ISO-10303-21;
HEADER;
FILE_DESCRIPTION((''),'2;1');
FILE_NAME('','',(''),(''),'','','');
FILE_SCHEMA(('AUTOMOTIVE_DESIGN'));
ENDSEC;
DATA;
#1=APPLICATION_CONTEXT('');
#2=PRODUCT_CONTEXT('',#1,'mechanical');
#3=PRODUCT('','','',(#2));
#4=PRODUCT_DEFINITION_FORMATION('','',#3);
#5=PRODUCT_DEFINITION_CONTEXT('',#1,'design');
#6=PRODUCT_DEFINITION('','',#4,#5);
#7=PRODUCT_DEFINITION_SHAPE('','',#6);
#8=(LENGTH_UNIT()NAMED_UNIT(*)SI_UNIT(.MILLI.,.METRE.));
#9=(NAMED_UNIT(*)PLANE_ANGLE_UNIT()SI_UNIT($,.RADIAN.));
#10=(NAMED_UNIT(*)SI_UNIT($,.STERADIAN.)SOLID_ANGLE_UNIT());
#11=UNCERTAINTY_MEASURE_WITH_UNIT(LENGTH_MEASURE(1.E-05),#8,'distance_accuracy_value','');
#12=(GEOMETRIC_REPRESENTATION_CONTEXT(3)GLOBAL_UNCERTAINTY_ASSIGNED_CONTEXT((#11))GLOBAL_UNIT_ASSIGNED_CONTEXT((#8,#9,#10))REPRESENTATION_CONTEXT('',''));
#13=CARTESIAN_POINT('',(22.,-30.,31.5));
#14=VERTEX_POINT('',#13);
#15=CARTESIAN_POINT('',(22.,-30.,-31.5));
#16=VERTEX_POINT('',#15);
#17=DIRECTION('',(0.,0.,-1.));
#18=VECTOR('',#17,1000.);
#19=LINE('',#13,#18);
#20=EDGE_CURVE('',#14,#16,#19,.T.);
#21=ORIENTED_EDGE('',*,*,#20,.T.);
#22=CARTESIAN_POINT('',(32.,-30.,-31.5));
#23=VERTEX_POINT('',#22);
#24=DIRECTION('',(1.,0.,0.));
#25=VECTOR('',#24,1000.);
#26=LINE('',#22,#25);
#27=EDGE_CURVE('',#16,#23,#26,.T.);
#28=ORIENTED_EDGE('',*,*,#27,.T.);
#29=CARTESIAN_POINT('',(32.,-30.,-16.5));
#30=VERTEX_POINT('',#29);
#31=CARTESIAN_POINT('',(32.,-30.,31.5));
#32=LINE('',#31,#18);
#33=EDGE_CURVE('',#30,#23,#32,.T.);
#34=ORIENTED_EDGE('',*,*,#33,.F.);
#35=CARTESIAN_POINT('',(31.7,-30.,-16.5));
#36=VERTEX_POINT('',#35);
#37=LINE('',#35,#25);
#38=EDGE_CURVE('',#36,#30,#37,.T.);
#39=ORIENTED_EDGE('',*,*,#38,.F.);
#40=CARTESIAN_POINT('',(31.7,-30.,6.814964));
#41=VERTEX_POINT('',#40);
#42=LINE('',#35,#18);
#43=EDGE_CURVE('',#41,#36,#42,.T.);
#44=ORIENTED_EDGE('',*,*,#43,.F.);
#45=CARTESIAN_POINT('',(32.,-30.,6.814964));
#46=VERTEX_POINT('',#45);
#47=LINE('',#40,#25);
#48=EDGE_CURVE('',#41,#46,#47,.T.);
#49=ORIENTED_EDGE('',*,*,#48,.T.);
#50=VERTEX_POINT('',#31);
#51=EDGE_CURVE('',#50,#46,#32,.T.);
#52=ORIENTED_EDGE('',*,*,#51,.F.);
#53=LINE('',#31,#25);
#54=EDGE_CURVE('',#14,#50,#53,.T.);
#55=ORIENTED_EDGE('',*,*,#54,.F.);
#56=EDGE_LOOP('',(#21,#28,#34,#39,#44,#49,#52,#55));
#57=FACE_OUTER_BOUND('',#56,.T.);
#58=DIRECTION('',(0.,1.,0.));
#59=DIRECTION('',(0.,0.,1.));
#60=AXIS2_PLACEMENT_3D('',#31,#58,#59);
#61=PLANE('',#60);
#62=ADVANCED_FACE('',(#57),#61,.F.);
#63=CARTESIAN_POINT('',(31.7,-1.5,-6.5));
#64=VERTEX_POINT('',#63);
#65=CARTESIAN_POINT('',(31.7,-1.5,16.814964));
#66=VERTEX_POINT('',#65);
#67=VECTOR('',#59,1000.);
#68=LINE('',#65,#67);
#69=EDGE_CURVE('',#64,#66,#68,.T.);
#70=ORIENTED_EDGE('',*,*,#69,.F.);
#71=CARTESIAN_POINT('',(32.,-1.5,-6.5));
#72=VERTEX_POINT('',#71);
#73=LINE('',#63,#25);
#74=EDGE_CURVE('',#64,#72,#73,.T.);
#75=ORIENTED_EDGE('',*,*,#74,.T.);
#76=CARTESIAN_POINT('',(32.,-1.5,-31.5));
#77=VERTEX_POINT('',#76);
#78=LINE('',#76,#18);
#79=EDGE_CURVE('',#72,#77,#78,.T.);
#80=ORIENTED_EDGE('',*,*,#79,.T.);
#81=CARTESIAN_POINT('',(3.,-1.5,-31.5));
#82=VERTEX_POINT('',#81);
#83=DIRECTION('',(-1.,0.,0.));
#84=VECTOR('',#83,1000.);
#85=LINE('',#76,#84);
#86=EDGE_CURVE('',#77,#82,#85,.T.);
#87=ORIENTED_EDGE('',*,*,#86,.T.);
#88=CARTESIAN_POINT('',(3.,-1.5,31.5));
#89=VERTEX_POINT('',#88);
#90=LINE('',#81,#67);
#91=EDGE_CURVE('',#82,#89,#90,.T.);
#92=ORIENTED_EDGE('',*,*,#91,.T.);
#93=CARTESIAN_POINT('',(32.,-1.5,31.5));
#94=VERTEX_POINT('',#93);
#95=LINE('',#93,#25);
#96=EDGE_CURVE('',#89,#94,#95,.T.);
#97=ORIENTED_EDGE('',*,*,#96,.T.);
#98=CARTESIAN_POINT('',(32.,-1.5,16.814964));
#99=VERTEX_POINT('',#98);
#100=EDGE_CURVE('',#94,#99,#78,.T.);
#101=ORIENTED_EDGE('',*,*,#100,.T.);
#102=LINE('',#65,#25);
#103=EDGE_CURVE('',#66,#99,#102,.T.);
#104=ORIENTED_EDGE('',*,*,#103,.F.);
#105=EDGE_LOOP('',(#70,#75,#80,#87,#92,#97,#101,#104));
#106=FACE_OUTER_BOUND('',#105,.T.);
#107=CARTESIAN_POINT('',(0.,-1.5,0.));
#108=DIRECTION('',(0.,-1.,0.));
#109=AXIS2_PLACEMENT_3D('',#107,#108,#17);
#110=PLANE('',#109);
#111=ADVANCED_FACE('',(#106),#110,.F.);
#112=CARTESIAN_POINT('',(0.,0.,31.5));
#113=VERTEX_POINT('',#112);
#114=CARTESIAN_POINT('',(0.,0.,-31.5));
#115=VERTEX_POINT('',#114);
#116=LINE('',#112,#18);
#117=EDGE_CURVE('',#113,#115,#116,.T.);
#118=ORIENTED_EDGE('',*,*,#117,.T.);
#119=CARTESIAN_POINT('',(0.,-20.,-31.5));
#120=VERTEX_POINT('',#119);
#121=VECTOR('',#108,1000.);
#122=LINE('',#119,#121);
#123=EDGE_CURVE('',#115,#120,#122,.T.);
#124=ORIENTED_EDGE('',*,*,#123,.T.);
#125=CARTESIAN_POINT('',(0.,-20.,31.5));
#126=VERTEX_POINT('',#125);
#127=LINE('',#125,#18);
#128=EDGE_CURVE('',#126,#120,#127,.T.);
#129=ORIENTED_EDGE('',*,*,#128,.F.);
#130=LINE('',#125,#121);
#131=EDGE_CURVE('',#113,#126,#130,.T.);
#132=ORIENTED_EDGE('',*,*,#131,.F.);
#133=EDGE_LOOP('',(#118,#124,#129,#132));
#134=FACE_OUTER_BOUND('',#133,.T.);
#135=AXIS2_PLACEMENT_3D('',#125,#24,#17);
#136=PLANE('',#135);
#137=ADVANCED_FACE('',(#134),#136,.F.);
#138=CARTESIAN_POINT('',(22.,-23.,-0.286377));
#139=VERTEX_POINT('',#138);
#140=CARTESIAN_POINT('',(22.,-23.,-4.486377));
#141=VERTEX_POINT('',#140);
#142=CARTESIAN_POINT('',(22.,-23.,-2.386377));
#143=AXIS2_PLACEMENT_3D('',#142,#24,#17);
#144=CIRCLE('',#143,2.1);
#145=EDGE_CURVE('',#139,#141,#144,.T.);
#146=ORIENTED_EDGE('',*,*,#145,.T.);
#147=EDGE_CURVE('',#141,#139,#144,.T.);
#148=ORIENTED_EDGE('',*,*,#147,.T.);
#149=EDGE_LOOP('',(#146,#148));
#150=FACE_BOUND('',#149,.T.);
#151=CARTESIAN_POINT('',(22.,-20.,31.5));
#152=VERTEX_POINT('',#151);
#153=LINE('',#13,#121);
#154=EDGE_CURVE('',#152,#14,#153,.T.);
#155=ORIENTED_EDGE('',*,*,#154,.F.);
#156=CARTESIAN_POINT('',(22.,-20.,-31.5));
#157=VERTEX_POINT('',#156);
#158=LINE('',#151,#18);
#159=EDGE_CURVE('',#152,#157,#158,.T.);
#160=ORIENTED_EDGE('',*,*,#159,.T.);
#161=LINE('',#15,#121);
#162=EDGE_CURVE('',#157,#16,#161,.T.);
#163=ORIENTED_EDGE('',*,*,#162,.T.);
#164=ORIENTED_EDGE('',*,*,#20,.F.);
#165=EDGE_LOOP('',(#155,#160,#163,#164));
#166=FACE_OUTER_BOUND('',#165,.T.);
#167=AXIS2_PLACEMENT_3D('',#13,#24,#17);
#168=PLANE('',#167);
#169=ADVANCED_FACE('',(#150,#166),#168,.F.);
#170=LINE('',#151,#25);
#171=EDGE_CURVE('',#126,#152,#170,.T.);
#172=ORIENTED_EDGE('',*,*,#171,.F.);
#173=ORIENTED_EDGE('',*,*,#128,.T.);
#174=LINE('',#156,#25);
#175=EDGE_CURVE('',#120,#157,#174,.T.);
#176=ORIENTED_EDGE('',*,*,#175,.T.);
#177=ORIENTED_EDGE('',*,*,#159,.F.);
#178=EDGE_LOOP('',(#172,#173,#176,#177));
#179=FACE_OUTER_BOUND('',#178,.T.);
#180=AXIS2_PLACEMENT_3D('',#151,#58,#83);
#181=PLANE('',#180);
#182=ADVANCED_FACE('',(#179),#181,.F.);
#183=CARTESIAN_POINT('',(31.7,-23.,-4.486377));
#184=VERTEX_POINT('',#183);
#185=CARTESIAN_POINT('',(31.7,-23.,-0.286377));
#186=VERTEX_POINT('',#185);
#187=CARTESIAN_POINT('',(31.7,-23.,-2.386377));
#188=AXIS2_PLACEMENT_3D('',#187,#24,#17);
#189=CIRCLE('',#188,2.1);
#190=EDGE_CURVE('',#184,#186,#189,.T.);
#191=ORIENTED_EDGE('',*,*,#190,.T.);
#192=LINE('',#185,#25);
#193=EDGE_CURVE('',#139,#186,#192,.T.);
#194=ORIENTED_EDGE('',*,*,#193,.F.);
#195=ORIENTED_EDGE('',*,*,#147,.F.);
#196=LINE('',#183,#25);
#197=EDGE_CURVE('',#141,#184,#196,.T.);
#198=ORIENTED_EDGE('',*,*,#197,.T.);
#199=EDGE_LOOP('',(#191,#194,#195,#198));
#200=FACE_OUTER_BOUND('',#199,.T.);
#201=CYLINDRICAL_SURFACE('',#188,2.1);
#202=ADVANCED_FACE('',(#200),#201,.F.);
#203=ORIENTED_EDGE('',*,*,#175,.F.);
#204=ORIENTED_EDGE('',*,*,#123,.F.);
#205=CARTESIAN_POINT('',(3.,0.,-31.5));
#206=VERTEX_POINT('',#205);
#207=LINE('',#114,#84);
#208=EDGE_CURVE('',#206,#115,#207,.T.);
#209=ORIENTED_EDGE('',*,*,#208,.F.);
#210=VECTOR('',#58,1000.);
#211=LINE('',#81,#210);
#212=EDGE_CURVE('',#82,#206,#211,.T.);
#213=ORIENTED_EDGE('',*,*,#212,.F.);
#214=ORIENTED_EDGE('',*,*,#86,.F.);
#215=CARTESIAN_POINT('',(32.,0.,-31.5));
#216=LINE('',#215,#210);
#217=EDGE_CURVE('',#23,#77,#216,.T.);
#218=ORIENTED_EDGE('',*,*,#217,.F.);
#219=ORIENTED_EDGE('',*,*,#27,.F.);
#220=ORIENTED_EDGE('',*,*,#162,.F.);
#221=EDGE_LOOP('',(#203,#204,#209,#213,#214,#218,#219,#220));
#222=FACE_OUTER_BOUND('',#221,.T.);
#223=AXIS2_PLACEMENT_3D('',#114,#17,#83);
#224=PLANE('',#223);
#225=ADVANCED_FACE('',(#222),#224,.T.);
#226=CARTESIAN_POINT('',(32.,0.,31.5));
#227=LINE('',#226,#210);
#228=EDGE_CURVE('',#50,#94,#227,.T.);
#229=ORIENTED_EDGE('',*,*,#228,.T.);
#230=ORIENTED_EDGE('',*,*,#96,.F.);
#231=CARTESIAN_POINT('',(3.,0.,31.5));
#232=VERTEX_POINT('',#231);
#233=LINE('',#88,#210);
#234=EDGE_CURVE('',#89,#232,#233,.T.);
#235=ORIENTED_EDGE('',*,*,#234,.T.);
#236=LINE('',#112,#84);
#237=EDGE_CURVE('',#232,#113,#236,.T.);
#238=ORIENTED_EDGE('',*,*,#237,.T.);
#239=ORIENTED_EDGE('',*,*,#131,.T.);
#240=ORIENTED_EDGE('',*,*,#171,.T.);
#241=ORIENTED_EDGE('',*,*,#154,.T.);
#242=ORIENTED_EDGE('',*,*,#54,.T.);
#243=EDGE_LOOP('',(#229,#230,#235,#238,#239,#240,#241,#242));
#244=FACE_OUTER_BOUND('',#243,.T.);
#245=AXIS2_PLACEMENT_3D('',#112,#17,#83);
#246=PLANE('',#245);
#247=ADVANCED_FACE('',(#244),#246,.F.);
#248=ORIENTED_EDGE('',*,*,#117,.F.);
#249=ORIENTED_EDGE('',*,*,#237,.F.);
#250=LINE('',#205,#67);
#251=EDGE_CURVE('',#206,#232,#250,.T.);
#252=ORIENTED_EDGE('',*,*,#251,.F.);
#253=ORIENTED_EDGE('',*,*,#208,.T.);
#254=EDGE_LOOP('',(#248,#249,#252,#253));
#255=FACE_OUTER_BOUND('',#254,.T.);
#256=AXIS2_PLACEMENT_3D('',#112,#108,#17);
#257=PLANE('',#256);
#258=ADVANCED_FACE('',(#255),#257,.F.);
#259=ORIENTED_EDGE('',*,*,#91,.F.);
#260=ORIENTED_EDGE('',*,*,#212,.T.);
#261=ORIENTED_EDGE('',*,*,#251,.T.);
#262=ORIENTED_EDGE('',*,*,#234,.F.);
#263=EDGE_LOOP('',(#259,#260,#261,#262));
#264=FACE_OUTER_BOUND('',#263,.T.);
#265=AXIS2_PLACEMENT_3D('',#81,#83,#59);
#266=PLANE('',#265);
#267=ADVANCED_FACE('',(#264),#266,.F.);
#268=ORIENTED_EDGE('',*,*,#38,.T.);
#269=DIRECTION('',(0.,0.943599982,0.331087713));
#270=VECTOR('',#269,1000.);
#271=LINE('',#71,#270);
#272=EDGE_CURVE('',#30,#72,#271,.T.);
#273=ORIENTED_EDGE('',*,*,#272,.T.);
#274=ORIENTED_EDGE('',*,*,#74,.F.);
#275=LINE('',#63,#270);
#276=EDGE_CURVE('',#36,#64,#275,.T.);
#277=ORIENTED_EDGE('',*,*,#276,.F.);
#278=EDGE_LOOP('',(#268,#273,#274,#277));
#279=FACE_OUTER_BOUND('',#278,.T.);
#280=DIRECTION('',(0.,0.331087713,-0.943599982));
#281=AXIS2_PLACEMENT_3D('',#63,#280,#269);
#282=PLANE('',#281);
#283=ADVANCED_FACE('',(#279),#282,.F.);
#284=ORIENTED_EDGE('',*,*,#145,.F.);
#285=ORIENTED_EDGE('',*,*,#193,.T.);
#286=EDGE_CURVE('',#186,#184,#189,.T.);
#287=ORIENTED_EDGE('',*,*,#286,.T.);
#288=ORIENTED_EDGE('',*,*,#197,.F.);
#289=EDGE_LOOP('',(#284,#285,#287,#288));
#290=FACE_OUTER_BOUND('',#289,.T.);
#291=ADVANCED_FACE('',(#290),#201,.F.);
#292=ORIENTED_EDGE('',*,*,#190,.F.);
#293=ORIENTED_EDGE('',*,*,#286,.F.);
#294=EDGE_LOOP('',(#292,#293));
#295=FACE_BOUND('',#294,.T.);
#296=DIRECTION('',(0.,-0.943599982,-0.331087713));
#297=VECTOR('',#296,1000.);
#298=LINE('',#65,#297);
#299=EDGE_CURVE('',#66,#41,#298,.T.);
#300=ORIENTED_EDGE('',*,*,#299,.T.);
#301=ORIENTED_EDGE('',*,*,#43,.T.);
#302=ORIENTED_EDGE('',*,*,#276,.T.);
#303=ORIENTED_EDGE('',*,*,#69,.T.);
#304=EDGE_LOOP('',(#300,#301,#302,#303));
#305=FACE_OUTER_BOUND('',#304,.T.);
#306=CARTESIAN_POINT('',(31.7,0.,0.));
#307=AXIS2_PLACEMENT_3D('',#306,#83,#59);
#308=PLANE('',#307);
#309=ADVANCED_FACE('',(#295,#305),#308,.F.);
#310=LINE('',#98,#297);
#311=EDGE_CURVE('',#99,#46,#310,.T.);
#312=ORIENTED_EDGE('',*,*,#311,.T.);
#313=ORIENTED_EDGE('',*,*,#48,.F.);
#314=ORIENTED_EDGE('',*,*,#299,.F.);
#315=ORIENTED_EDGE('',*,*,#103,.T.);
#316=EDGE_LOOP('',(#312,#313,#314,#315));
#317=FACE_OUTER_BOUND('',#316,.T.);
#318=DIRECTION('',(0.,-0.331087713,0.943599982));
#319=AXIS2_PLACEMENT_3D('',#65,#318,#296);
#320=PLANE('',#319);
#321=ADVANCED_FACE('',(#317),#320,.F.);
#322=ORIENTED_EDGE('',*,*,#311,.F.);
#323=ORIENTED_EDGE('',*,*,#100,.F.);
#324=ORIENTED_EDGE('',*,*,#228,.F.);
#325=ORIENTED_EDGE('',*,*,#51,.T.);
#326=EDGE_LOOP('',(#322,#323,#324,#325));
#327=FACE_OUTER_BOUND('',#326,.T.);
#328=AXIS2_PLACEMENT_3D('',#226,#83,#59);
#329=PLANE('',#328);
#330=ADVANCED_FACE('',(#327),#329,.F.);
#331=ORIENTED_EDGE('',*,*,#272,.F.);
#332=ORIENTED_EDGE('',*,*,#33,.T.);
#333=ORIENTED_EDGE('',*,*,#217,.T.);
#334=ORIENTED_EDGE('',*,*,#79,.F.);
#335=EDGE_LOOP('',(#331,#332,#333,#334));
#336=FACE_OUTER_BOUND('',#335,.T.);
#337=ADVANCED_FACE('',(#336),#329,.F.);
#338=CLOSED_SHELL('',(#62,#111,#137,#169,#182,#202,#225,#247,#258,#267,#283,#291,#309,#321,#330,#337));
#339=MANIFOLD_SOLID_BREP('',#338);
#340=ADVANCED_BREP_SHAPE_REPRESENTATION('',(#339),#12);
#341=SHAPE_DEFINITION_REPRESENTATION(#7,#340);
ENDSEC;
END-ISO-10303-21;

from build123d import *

# Parameters (mm, degrees)
EXTRUDE_1_DEPTH     = 31.5
SKETCH_2_W          = 29
SKETCH_2_H          = 63
CUT_EXTRUDE_1_DEPTH = 1.5
CUT_EXTRUDE_2_DEPTH = 0.3
HOLE_WIZARD_M5_1_D  = 4.2


with BuildPart() as part:
    # 草图1 → 凸台-拉伸1 (new, symmetric)
    with BuildSketch(Plane.XY):
        Polygon((0, 0), (32, 0), (32, -30), (22, -30), (22, -20), (0, -20), align=None)
    extrude(amount=EXTRUDE_1_DEPTH, both=True)

    # 草图2 → 切除-拉伸1 (cut)
    with BuildSketch(Plane(origin=(0, 0, 0), x_dir=(1, 0, 0), z_dir=(0, 1, 0))):
        with Locations((17.5, 0)):
            Rectangle(SKETCH_2_W, SKETCH_2_H)
    extrude(amount=-CUT_EXTRUDE_1_DEPTH, mode=Mode.SUBTRACT)

    # 草图3 → 切除-拉伸2 (cut)
    with BuildSketch(Plane(origin=(32, 0, 0), x_dir=(0, 0, -1), z_dir=(1, 0, 0))):
        Polygon((-16.814964409, -1.5), (-6.814964409, -30), (16.5, -30), (6.5, -1.5), align=None)
    extrude(amount=-CUT_EXTRUDE_2_DEPTH, mode=Mode.SUBTRACT)

    # M5 螺纹孔1 (through all)
    with Locations(Plane(origin=(31.7, -23, -2.386377444), x_dir=(0, 0, 1), z_dir=(1, 0, 0))):
        with Locations((0, 0)):
            Hole(HOLE_WIZARD_M5_1_D / 2)


solid = part.part
